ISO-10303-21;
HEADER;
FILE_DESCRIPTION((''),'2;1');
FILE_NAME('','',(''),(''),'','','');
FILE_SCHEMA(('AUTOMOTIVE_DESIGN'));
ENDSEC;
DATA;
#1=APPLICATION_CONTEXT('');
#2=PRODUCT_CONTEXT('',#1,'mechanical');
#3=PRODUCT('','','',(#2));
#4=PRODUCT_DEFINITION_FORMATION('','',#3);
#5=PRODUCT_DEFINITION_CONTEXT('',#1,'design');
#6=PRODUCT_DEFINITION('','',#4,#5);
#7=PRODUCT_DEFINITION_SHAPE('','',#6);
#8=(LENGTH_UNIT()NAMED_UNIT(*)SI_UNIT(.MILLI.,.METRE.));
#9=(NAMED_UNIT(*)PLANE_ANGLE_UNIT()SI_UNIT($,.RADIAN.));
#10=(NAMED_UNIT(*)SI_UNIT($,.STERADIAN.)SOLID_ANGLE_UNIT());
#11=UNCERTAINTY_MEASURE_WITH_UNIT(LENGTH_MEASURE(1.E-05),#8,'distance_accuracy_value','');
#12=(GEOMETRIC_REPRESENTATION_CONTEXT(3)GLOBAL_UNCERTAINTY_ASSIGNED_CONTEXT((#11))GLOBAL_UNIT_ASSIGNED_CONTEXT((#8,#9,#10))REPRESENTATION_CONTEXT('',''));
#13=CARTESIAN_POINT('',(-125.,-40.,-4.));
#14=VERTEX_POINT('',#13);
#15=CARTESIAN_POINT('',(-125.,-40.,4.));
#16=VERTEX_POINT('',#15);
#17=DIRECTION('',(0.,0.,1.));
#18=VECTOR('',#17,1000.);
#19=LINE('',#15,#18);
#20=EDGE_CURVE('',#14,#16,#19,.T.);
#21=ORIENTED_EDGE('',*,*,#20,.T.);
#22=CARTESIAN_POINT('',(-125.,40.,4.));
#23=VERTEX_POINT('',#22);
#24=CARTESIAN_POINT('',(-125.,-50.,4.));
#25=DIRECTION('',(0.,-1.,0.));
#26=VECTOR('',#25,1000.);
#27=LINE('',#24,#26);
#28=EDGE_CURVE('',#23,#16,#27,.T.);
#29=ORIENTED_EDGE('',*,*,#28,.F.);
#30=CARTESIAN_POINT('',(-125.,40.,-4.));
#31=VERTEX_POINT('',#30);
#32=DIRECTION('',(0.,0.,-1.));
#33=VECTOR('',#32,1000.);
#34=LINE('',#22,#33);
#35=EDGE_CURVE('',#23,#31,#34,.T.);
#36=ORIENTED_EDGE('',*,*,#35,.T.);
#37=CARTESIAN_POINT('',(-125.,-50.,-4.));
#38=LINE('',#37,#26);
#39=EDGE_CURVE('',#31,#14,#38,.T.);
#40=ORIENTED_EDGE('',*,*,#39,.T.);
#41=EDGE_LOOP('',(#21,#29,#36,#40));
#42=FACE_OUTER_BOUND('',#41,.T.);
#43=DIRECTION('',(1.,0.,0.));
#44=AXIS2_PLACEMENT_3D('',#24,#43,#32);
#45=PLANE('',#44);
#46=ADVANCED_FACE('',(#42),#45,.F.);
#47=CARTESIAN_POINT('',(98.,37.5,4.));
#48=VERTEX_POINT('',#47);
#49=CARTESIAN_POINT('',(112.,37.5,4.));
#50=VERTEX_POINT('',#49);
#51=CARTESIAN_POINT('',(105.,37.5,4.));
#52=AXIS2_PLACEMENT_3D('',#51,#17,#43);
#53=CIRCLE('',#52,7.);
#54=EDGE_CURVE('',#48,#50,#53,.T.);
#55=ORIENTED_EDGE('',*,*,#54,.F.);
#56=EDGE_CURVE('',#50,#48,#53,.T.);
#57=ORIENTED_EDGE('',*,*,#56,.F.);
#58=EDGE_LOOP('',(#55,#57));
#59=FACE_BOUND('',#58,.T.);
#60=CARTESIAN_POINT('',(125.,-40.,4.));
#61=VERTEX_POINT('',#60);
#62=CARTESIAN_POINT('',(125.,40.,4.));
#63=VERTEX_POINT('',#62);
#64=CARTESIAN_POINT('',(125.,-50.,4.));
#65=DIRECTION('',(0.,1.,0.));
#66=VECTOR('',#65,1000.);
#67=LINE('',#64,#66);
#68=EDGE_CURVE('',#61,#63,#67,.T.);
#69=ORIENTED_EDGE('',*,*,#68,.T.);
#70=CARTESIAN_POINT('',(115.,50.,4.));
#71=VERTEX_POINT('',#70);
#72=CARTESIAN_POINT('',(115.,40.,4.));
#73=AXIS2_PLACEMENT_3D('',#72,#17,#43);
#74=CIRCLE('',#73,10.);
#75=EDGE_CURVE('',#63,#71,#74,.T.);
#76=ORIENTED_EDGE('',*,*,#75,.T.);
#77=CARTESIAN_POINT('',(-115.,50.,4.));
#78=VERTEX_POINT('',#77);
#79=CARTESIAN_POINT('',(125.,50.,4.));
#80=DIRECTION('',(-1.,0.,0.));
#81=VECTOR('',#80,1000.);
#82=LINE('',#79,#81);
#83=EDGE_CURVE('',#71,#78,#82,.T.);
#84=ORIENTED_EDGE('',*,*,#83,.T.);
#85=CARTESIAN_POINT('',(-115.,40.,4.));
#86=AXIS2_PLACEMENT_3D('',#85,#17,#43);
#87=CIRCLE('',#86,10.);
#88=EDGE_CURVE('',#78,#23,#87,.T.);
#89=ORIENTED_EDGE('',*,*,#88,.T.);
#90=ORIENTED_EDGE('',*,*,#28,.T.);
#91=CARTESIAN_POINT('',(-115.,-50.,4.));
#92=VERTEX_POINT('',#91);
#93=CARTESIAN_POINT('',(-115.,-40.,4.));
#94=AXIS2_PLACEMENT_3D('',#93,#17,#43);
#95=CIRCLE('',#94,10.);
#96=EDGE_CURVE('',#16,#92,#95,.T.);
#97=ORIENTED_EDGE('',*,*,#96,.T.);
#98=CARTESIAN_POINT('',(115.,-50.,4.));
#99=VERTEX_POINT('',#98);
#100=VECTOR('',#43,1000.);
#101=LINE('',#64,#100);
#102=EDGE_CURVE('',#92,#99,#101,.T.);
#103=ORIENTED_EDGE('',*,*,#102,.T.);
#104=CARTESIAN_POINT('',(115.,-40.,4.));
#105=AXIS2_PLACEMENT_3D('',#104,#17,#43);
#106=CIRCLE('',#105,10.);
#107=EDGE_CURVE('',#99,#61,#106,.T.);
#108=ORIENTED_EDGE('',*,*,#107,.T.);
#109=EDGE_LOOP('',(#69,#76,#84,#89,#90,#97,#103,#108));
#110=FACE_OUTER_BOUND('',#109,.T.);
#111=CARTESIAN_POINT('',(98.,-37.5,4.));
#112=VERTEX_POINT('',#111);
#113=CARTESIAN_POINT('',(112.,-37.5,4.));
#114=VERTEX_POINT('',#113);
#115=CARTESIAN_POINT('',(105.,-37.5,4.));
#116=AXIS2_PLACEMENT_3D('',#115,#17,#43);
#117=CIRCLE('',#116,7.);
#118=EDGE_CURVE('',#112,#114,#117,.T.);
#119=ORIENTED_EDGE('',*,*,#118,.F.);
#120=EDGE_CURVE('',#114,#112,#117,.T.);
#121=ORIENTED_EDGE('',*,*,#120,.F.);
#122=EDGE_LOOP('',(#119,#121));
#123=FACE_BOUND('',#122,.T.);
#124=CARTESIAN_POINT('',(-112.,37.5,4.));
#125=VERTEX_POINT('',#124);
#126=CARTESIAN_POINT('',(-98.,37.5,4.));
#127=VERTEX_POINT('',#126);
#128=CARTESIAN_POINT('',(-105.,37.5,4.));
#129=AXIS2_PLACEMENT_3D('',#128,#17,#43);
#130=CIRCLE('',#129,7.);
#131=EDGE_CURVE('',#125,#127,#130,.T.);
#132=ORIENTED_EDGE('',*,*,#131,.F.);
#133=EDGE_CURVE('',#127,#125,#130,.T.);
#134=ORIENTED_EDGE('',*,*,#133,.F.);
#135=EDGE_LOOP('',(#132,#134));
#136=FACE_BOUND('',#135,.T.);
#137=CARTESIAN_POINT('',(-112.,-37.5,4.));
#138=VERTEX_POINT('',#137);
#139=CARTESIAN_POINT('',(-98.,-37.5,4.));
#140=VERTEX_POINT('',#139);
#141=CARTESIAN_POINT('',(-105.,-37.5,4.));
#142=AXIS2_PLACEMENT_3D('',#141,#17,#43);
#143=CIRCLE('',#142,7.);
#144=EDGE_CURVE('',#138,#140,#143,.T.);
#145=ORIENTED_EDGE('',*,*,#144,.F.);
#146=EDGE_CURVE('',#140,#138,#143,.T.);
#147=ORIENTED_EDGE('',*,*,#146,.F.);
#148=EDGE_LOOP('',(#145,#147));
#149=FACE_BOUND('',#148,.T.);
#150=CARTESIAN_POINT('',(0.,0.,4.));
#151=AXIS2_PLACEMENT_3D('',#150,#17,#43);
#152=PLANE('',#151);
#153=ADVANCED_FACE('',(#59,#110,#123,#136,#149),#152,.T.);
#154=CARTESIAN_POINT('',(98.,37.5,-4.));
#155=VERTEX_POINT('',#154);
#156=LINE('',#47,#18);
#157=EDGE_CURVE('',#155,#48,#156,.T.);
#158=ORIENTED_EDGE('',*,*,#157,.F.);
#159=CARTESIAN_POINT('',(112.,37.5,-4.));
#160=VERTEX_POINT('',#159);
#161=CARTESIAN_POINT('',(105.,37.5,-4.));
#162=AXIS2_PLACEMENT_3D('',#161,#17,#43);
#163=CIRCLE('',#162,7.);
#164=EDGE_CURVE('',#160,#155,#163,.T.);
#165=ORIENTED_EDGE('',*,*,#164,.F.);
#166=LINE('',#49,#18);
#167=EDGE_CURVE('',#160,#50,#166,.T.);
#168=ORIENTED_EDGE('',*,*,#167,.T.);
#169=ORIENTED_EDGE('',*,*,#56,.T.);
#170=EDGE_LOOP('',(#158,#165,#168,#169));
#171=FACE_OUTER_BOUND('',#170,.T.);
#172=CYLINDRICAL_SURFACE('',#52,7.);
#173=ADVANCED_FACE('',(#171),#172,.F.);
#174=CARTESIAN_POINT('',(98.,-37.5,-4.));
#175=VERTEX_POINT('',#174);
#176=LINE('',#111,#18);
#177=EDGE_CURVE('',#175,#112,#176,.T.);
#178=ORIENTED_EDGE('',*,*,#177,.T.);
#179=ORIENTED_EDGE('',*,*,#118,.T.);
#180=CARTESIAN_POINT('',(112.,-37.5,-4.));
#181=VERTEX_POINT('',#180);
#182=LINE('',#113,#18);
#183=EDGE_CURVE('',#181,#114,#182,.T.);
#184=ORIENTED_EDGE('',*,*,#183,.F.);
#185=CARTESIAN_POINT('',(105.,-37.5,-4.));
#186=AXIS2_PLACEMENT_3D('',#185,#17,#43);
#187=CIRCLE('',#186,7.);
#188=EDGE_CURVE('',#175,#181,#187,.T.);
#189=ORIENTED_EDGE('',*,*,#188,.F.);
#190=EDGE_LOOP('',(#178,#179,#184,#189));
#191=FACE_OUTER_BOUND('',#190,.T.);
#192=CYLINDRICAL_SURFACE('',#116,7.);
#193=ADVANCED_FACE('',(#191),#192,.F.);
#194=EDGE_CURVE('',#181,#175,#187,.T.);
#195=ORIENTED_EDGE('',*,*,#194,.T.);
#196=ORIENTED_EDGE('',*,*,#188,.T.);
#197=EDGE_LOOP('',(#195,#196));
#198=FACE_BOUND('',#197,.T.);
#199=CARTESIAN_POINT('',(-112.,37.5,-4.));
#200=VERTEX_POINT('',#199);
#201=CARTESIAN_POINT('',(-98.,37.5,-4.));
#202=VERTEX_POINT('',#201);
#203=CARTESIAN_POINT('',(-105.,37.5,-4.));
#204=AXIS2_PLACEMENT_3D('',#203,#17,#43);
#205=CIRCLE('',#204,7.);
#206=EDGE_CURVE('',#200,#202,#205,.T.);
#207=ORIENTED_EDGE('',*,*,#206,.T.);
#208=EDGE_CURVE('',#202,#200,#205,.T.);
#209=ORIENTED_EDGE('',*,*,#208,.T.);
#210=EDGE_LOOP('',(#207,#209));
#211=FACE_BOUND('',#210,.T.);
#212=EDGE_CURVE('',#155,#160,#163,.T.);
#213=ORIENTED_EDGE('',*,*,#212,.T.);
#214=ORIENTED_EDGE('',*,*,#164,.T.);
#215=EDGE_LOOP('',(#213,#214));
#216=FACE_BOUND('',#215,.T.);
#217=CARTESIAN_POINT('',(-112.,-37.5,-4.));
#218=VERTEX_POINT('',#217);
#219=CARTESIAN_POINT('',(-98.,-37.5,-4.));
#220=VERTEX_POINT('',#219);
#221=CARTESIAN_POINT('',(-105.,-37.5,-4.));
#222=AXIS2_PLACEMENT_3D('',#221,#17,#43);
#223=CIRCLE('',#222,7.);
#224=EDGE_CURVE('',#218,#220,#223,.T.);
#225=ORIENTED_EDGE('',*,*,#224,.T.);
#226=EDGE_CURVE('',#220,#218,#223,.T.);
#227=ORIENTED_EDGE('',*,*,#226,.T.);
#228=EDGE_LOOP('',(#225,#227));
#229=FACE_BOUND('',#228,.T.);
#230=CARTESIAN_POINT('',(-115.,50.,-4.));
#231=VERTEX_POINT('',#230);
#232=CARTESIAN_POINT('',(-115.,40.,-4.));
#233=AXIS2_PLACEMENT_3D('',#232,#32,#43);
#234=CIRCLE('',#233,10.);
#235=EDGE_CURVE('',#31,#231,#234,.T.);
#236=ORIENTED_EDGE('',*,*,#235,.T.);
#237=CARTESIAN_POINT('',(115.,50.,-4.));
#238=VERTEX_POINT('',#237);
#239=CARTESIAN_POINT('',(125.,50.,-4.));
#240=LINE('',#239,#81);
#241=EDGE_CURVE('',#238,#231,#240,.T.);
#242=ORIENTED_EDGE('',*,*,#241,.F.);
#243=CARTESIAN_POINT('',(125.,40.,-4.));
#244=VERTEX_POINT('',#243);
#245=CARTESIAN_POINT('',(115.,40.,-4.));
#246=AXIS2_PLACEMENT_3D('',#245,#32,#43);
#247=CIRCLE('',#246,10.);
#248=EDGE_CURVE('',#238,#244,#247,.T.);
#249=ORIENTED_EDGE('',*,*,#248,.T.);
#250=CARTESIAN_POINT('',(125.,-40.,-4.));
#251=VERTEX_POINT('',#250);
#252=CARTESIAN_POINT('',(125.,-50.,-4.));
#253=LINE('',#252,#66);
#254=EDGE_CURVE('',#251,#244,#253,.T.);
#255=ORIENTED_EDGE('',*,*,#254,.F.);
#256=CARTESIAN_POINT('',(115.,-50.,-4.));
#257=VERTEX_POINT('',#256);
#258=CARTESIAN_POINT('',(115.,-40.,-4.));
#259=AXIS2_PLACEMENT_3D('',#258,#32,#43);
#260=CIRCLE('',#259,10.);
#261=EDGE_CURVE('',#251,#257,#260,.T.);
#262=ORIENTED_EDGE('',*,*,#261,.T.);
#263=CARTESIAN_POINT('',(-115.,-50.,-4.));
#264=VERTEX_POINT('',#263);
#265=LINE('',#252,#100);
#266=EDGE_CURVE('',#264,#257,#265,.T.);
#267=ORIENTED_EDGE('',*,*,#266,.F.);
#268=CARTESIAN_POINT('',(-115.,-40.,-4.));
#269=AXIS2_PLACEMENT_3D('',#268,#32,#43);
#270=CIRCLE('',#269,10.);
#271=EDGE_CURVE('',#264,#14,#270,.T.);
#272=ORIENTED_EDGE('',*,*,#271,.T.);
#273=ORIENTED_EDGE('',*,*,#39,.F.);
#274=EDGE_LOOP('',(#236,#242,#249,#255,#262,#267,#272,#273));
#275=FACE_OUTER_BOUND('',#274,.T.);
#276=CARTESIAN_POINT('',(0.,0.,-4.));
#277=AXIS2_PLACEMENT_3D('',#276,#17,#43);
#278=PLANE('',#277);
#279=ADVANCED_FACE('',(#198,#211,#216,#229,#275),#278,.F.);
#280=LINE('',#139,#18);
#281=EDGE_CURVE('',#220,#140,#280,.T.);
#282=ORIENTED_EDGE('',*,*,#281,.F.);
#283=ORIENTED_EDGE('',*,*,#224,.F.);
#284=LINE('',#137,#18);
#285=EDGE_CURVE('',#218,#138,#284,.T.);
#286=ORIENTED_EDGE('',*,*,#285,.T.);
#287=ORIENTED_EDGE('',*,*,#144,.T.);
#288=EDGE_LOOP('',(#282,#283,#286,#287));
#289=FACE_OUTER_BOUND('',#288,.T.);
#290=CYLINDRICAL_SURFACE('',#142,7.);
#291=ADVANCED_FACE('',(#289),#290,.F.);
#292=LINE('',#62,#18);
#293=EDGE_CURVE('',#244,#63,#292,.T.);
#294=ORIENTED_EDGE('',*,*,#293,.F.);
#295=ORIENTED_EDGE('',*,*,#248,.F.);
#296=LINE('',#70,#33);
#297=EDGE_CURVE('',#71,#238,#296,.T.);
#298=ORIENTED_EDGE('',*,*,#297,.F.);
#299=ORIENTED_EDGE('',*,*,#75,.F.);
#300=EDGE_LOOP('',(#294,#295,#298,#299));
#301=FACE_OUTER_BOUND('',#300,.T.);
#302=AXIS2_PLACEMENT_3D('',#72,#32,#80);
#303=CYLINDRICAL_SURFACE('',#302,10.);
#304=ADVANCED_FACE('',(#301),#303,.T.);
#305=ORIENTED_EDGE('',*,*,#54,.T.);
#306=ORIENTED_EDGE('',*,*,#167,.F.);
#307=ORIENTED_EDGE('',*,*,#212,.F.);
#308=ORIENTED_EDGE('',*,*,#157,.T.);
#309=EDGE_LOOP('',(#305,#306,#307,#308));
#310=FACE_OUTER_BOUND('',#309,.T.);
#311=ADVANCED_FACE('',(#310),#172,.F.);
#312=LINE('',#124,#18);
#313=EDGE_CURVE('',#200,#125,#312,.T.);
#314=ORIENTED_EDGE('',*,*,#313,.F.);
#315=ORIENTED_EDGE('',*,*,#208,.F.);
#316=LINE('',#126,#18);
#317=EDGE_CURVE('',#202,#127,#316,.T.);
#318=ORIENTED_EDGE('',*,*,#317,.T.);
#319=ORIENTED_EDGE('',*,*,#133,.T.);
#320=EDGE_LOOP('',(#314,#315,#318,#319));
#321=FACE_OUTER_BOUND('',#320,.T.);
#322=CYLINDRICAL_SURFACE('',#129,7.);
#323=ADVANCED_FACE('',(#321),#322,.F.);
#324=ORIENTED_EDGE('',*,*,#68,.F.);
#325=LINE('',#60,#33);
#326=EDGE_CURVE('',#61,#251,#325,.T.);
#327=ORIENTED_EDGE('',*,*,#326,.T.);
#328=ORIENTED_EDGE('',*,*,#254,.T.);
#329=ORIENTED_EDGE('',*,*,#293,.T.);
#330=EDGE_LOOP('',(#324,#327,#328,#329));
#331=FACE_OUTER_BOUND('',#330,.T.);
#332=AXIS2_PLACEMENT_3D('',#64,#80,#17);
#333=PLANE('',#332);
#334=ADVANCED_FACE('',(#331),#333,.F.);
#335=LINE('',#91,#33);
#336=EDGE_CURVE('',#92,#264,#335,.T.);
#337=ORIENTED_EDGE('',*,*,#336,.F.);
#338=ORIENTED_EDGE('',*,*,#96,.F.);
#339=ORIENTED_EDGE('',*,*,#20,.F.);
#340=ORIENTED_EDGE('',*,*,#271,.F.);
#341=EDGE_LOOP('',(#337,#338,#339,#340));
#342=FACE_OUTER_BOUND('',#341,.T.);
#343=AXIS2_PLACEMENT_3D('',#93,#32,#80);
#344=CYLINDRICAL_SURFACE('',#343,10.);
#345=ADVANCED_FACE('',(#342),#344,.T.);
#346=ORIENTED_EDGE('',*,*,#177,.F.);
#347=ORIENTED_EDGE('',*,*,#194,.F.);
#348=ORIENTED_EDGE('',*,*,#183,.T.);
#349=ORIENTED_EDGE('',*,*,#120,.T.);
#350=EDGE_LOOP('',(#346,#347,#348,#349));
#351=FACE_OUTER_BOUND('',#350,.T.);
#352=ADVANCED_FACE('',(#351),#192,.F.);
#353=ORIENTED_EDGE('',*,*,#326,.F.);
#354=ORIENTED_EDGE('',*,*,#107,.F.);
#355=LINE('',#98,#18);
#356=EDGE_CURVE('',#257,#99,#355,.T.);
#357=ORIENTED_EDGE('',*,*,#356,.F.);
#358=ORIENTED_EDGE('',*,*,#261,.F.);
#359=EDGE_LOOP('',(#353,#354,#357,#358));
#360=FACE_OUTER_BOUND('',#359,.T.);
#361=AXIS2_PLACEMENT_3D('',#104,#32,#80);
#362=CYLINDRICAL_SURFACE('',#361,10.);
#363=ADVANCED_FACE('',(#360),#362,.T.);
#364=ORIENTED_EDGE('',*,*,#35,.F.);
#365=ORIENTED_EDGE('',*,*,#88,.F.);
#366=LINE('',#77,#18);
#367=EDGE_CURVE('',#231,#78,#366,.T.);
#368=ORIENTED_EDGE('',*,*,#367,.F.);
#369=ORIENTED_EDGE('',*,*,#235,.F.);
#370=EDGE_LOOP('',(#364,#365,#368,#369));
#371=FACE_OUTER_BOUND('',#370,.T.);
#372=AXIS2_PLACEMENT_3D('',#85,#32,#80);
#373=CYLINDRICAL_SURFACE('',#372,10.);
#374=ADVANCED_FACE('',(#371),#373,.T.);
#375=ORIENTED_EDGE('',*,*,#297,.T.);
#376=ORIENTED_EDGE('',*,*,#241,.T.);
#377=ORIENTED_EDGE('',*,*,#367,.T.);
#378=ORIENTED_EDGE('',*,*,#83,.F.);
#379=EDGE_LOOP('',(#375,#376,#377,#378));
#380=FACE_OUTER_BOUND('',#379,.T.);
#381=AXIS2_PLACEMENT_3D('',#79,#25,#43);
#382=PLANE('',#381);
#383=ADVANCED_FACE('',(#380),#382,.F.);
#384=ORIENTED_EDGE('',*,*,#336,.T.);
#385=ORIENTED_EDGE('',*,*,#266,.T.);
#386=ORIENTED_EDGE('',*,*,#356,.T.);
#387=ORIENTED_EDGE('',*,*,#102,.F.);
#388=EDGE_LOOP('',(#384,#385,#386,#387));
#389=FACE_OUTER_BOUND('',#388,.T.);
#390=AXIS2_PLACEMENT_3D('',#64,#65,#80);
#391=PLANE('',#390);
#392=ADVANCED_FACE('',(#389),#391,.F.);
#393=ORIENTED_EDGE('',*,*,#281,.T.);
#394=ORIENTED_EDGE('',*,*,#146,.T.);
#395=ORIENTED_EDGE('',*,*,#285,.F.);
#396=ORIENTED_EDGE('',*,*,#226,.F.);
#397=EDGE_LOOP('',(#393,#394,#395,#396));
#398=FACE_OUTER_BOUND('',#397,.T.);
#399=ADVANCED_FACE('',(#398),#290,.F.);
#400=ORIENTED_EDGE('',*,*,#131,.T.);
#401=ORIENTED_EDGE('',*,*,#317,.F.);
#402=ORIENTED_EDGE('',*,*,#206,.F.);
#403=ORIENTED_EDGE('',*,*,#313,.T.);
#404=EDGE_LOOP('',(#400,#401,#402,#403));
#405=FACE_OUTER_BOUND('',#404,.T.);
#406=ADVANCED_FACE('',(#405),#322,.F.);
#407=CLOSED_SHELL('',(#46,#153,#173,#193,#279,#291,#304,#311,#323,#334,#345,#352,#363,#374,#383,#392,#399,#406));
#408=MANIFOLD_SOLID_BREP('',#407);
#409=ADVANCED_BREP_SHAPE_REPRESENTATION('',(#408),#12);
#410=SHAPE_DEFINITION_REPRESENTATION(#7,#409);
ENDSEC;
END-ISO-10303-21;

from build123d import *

# Parameters (mm, degrees)
SKETCH1_W                  = 250
SKETCH1_H                  = 100
BOSS_EXTRUDE1_DEPTH        = 4
F_14_0_14_DIAMETER_HOLE1_D = 14
FILLET1_R                  = 10


with BuildPart() as part:
    # Sketch1 → Boss-Extrude1 (new, symmetric)
    with BuildSketch(Plane.XY):
        Rectangle(SKETCH1_W, SKETCH1_H)
    extrude(amount=BOSS_EXTRUDE1_DEPTH, both=True)

    # Ø14.0 (14) Diameter Hole1 (through all)
    with Locations(Plane.XY.offset(4)):
        with Locations((-105, 37.5), (105, 37.5), (105, -37.5), (-105, -37.5)):
            Hole(F_14_0_14_DIAMETER_HOLE1_D / 2)

    # Fillet1
    fillet1_edges = [part.edges().sort_by_distance(p)[0] for p in [
        (-125, 50, 0),
        (125, 50, 0),
        (125, -50, 0),
        (-125, -50, 0),
    ]]
    fillet(fillet1_edges, radius=FILLET1_R)


solid = part.part
